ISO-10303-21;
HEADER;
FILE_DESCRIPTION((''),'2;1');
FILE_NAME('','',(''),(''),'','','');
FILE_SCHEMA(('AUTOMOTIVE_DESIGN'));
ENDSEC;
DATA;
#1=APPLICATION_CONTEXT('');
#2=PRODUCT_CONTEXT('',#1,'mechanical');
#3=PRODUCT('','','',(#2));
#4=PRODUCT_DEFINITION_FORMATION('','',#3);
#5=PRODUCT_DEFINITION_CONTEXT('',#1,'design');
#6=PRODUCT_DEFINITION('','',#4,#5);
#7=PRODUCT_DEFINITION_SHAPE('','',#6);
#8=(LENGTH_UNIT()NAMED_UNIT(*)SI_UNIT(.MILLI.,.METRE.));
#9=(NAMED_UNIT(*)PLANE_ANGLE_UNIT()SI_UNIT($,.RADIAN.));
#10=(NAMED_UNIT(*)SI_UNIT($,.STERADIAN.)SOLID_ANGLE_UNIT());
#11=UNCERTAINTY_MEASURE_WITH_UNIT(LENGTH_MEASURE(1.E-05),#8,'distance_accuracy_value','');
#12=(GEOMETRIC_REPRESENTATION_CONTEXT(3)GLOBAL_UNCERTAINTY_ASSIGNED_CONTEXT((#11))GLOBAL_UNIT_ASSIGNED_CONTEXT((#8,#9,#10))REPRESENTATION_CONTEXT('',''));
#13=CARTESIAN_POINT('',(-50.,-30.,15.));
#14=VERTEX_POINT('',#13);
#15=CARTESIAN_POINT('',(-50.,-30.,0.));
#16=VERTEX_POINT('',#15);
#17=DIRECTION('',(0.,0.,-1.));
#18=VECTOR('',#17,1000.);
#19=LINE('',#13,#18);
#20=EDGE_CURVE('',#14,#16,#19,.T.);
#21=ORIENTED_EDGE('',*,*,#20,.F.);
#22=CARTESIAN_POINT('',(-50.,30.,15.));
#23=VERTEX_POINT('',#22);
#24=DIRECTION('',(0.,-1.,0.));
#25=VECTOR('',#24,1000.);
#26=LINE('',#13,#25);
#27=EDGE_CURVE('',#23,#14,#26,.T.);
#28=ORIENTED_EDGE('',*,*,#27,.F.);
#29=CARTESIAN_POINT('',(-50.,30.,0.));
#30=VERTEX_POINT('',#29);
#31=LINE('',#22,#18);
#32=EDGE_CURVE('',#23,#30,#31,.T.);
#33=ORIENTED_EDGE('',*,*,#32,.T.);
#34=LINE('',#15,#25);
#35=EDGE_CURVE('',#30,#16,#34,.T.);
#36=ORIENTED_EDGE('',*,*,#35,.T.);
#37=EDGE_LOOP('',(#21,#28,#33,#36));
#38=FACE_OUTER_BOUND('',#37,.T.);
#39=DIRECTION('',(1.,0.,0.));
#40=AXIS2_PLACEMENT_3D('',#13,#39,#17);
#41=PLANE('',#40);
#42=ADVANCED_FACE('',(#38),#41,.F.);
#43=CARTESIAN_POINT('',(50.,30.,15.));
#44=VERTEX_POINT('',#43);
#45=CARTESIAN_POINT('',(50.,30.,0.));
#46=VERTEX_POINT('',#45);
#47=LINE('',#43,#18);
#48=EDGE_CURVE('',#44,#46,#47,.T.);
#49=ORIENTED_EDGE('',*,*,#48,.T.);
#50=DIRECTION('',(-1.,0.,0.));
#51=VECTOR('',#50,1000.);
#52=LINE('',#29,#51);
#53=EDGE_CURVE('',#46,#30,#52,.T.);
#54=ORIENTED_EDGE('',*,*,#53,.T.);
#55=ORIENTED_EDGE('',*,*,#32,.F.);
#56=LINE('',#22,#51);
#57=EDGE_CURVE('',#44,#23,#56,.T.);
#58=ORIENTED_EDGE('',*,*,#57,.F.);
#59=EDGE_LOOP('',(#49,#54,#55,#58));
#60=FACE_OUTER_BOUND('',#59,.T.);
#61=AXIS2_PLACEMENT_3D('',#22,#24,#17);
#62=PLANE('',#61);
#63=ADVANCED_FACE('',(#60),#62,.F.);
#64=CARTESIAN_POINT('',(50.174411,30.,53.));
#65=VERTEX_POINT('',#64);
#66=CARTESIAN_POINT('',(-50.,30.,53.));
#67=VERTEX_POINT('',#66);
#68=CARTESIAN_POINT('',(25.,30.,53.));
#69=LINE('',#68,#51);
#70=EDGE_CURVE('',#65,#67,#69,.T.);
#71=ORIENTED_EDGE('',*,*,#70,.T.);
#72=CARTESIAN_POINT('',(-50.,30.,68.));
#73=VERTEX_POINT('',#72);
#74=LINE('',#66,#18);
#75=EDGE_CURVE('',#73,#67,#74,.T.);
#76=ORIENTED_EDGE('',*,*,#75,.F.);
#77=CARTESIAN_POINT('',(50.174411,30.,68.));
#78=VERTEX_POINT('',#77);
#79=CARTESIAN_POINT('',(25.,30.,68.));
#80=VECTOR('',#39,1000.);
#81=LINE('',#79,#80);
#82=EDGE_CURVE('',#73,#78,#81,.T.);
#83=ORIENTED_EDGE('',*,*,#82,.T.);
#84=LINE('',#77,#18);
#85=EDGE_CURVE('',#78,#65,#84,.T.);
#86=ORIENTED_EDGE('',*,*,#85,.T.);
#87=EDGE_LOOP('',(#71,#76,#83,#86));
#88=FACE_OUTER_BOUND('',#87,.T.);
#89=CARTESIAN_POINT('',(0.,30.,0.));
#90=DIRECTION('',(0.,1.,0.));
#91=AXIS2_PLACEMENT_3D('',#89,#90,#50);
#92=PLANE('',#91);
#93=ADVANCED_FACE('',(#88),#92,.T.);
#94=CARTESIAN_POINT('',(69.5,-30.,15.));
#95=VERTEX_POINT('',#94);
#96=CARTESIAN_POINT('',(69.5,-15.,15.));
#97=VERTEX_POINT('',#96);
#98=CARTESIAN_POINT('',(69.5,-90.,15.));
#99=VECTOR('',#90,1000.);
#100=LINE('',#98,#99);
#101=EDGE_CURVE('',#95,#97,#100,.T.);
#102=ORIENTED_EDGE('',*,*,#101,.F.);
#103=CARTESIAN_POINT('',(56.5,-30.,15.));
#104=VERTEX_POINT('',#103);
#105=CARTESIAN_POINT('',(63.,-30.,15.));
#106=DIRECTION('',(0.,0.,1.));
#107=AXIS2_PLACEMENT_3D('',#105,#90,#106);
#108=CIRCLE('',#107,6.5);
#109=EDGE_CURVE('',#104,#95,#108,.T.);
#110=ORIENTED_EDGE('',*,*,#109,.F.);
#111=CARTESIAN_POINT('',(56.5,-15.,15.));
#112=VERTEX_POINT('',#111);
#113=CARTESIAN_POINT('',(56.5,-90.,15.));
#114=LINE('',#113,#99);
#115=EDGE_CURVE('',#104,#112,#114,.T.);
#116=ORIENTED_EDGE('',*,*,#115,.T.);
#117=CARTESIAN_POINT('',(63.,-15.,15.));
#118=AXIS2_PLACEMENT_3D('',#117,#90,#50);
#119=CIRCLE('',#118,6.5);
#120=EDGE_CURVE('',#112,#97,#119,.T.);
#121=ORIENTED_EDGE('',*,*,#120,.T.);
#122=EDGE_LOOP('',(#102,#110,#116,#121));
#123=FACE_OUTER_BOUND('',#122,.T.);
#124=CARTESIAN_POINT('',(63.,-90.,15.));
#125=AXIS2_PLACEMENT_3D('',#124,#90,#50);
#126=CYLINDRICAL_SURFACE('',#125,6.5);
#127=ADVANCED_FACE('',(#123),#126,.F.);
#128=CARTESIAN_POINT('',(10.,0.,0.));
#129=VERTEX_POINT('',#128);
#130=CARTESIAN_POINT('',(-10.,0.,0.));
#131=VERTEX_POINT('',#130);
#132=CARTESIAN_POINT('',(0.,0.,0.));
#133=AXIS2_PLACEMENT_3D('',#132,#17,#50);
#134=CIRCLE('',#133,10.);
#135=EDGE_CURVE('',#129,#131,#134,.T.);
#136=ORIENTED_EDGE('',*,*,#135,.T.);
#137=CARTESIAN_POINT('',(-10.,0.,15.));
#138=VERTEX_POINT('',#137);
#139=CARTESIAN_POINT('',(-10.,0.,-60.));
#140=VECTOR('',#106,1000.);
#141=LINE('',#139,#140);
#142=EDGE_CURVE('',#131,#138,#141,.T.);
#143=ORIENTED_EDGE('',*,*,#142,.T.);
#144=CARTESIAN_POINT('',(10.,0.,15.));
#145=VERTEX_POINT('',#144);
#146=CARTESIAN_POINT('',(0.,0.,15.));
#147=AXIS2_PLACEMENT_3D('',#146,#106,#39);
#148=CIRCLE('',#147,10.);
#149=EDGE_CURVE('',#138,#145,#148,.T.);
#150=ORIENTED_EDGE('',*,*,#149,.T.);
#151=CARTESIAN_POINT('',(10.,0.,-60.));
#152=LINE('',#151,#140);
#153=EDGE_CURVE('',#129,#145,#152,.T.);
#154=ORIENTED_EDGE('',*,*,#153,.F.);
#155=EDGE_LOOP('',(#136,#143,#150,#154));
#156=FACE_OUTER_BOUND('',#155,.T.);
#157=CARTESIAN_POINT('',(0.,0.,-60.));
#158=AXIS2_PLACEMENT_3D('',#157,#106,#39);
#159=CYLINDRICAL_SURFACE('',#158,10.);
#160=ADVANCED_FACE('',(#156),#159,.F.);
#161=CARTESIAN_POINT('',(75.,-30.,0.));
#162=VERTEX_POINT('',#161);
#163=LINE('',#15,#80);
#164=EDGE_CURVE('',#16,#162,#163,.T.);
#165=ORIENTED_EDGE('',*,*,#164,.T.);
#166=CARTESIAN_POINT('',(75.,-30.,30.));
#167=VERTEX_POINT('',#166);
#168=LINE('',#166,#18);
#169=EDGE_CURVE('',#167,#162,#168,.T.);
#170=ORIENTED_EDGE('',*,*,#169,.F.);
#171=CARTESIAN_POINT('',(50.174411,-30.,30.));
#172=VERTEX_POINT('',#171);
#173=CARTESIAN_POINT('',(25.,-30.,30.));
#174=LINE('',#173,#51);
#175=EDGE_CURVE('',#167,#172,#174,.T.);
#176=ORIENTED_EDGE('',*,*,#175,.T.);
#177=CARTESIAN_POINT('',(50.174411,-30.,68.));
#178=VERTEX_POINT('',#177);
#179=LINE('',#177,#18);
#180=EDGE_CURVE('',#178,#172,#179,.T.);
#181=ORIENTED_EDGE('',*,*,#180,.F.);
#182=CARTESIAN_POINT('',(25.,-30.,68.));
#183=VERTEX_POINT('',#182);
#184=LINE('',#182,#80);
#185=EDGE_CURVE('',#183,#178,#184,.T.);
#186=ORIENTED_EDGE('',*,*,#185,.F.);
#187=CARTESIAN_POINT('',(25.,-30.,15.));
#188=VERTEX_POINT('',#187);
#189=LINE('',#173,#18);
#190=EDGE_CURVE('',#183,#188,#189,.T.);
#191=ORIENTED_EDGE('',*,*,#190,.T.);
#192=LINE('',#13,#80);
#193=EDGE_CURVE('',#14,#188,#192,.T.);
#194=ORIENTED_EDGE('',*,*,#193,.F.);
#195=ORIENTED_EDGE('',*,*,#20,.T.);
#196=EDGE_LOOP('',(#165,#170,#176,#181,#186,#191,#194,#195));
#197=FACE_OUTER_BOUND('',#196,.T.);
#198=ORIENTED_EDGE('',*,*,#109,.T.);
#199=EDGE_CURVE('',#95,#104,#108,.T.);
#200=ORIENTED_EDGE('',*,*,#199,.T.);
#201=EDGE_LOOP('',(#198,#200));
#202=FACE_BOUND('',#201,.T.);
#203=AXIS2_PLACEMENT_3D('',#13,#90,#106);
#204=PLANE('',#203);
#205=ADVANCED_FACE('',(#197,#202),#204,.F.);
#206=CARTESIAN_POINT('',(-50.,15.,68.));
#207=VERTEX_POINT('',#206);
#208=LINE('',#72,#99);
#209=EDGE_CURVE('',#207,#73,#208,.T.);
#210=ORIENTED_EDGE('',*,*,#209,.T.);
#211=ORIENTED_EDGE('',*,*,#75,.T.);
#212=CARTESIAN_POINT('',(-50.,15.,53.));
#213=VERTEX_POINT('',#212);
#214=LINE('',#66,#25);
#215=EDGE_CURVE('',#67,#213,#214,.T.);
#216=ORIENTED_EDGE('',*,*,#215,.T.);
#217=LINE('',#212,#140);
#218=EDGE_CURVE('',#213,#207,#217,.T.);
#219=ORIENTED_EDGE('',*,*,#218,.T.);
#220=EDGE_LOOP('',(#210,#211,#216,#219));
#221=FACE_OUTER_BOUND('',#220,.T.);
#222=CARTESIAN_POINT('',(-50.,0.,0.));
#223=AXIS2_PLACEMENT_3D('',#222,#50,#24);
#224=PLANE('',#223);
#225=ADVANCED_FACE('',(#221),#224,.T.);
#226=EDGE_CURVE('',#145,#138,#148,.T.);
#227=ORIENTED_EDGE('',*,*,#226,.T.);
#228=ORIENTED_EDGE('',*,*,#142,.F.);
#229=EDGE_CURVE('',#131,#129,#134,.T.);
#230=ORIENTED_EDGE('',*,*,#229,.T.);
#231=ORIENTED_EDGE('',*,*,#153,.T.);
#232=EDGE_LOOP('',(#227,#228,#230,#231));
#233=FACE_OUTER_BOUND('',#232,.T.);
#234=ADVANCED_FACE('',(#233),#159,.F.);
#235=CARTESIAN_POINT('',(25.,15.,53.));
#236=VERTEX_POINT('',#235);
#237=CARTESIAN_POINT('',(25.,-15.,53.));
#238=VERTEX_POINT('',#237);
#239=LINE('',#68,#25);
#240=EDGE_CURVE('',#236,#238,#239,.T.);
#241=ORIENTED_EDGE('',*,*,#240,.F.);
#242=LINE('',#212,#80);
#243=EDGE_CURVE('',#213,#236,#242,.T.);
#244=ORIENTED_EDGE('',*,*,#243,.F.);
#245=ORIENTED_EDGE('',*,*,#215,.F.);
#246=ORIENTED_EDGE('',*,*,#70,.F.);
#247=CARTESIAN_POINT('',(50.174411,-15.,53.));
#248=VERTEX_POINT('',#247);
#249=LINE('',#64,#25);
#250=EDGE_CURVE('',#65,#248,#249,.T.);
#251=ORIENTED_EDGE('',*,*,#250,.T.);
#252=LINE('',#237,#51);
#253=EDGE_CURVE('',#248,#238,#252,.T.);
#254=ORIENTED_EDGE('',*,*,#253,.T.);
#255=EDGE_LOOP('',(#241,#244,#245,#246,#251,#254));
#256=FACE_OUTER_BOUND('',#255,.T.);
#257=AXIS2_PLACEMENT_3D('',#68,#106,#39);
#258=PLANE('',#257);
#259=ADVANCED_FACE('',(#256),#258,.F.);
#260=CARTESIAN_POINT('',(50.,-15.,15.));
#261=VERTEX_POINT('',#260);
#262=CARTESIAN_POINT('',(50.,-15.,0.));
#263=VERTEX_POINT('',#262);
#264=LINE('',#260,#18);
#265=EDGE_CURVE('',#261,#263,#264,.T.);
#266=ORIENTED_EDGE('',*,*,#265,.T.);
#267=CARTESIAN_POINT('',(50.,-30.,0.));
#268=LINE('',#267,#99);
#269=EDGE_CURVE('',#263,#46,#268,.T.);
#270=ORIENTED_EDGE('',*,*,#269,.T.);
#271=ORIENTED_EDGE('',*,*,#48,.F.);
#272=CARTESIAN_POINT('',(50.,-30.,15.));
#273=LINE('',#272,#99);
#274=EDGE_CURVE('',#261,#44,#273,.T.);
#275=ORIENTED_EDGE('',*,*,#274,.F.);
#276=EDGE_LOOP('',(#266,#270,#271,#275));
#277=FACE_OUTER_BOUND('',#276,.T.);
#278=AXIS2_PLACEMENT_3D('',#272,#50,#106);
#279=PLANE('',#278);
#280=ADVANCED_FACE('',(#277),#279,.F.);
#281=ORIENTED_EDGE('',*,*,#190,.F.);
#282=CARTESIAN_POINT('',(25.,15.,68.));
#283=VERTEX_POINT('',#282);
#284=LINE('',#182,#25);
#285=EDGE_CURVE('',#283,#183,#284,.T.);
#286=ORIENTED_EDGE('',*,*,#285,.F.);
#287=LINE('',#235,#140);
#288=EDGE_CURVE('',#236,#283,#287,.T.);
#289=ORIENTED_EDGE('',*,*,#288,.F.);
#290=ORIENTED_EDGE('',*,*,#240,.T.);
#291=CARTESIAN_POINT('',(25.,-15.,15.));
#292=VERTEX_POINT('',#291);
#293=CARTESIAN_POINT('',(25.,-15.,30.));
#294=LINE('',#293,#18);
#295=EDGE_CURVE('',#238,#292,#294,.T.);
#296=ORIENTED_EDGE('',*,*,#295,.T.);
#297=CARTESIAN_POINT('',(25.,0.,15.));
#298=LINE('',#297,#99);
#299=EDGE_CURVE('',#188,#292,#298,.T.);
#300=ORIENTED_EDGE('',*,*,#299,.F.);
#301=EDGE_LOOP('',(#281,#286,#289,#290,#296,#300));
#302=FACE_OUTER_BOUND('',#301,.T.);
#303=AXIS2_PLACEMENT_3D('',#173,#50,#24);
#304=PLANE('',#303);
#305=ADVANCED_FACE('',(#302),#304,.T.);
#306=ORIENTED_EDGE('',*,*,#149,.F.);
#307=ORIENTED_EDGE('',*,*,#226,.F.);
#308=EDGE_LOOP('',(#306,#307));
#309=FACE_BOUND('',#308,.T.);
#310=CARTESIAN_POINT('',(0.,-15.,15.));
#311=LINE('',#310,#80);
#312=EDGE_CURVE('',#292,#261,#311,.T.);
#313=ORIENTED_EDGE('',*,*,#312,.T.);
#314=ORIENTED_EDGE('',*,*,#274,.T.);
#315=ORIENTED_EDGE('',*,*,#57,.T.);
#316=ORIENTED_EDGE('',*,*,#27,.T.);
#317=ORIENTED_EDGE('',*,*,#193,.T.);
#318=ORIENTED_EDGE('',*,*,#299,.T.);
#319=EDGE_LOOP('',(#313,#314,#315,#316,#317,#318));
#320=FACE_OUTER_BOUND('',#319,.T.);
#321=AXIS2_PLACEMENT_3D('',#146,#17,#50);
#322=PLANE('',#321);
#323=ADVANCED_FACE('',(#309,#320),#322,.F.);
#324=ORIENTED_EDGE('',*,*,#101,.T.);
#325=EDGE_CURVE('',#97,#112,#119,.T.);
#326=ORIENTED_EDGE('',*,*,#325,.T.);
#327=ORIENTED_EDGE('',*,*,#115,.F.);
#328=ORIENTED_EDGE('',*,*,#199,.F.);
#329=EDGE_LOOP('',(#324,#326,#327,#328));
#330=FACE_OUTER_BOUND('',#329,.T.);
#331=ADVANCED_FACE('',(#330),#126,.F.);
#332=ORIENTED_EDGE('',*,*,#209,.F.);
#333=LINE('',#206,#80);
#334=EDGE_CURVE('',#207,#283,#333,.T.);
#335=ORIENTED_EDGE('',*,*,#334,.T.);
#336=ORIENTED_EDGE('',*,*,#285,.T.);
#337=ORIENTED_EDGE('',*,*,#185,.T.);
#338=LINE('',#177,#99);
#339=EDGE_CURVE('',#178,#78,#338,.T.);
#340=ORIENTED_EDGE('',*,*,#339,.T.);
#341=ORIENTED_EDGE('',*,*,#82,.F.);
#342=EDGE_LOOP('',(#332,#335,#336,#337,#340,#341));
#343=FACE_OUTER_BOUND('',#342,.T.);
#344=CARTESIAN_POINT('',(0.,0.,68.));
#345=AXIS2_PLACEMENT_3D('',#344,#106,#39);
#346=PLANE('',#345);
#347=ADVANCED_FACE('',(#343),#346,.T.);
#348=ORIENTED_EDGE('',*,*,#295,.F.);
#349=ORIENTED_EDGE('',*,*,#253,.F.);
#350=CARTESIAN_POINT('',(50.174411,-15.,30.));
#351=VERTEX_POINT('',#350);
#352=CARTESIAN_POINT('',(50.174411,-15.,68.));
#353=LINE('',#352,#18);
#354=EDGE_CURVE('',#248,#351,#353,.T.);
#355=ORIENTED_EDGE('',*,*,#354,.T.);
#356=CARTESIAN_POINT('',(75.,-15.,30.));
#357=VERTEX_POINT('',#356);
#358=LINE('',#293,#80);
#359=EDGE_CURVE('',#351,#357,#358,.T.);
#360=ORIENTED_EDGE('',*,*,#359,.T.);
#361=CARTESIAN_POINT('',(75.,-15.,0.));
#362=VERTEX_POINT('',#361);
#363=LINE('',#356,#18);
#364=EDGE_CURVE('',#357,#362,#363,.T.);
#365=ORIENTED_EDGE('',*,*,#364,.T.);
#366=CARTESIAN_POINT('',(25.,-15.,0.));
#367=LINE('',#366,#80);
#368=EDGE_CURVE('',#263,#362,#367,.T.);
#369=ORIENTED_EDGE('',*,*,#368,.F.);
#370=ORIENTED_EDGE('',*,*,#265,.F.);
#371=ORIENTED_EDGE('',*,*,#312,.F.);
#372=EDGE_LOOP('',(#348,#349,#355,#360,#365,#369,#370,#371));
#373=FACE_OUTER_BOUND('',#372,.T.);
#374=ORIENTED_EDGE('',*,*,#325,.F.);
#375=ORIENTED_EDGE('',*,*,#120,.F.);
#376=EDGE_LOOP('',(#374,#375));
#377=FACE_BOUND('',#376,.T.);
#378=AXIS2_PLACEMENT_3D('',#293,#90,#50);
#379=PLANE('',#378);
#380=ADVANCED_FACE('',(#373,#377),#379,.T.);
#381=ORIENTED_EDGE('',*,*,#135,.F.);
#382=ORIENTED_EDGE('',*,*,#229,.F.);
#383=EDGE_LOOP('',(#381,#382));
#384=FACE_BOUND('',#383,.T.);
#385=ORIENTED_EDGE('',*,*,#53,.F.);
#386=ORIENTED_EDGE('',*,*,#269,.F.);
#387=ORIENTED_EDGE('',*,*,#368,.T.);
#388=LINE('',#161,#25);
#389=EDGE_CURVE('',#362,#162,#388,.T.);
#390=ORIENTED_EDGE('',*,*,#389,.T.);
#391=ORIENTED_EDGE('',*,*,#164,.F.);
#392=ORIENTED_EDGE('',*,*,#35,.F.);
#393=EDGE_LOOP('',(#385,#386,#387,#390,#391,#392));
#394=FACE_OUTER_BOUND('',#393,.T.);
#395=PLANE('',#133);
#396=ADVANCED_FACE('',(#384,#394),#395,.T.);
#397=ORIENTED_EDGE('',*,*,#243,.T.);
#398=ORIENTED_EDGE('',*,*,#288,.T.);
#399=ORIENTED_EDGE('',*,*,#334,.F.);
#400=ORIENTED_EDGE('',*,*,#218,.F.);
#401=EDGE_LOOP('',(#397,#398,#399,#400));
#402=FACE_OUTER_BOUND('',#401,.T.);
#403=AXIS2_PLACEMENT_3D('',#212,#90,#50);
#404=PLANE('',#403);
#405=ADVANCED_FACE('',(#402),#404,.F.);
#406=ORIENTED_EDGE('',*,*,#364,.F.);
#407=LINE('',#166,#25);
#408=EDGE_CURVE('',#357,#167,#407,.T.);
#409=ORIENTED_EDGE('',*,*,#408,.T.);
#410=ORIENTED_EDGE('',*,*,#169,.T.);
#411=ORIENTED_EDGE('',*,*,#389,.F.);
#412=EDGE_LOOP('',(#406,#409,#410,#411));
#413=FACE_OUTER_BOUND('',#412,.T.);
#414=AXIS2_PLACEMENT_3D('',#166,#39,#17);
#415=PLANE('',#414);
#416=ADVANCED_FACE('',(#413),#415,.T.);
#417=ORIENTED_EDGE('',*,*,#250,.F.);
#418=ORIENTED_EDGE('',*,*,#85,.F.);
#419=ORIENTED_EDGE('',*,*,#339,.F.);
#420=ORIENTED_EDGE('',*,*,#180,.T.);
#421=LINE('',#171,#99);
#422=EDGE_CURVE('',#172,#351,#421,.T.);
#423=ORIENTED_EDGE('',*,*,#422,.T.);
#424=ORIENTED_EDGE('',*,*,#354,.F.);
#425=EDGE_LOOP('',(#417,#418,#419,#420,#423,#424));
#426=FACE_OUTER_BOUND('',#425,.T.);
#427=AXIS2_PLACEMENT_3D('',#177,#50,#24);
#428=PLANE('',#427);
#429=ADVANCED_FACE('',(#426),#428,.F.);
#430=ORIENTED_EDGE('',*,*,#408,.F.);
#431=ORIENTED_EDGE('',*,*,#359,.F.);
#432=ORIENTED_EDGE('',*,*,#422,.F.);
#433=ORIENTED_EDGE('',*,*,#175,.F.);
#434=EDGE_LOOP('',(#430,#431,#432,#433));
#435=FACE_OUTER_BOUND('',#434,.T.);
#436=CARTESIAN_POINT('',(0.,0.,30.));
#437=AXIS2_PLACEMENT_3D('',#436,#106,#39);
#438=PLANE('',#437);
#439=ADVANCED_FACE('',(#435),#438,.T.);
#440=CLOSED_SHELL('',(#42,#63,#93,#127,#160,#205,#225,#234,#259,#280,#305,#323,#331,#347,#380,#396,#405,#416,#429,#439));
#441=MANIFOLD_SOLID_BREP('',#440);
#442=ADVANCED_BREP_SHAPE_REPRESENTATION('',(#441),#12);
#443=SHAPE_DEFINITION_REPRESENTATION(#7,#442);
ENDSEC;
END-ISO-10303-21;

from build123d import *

# Parameters (mm, degrees)
BASE_PLATE_SKETCH_W     = 100
BASE_PLATE_SKETCH_H     = 60
BASE_PLATE_DEPTH        = 15
UPRIGHT_BLOCK_SKETCH_W  = 50
UPRIGHT_BLOCK_SKETCH_H  = 15
UPRIGHT_BLOCK_DEPTH     = 30
SIDE_WALL_SKETCH_W      = 25.174411278
SIDE_WALL_SKETCH_H      = 15
SIDE_WALL_DEPTH         = 38
LOWER_ARM_SKETCH_W      = 25.174411278
LOWER_ARM_SKETCH_H      = 15
LOWER_ARM_DEPTH         = 45
UPPER_ARM_SKETCH_W      = 15
UPPER_ARM_SKETCH_H      = 15
UPPER_ARM_DEPTH         = 75
WALL_HOLE_SKETCH_R      = 6.5
WALL_THROUGH_HOLE_DEPTH = 75
BASE_HOLE_SKETCH_R      = 10
BASE_THROUGH_HOLE_DEPTH = 75


with BuildPart() as part:
    # Base Plate Sketch → Base Plate (new body)
    with BuildSketch(Plane.XY):
        Rectangle(BASE_PLATE_SKETCH_W, BASE_PLATE_SKETCH_H)
    extrude(amount=BASE_PLATE_DEPTH)

    # Upright Block Sketch → Upright Block (add)
    with BuildSketch(Plane(origin=(0, 0, 0), x_dir=(-1, 0, 0), z_dir=(0, 0, -1))):
        with Locations((-50, -22.5)):
            Rectangle(UPRIGHT_BLOCK_SKETCH_W, UPRIGHT_BLOCK_SKETCH_H)
    extrude(amount=-UPRIGHT_BLOCK_DEPTH)

    # Side Wall Sketch → Side Wall (add)
    with BuildSketch(Plane.XY.offset(30)):
        with Locations((37.587205639, -22.5)):
            Rectangle(SIDE_WALL_SKETCH_W, SIDE_WALL_SKETCH_H)
    extrude(amount=SIDE_WALL_DEPTH)

    # Lower Arm Sketch → Lower Arm (add)
    with BuildSketch(Plane(origin=(0, -15, 0), x_dir=(1, 0, 0), z_dir=(0, 1, 0))):
        with Locations((37.587205639, -60.5)):
            Rectangle(LOWER_ARM_SKETCH_W, LOWER_ARM_SKETCH_H)
    extrude(amount=LOWER_ARM_DEPTH)

    # Upper Arm Sketch → Upper Arm (add)
    with BuildSketch(Plane.ZY.offset(-25)):
        with Locations((60.5, 22.5)):
            Rectangle(UPPER_ARM_SKETCH_W, UPPER_ARM_SKETCH_H)
    extrude(amount=UPPER_ARM_DEPTH)

    # Wall Hole Sketch → Wall Through Hole (cut)
    with BuildSketch(Plane(origin=(0, -15, 0), x_dir=(1, 0, 0), z_dir=(0, 1, 0))):
        with Locations(Location((63, -15, 0), (0, 0, 180))):
            Circle(WALL_HOLE_SKETCH_R)
    extrude(amount=-WALL_THROUGH_HOLE_DEPTH, mode=Mode.SUBTRACT)

    # Base Hole Sketch → Base Through Hole (cut)
    with BuildSketch(Plane.XY.offset(15)):
        Circle(BASE_HOLE_SKETCH_R)
    extrude(amount=-BASE_THROUGH_HOLE_DEPTH, mode=Mode.SUBTRACT)


solid = part.part
